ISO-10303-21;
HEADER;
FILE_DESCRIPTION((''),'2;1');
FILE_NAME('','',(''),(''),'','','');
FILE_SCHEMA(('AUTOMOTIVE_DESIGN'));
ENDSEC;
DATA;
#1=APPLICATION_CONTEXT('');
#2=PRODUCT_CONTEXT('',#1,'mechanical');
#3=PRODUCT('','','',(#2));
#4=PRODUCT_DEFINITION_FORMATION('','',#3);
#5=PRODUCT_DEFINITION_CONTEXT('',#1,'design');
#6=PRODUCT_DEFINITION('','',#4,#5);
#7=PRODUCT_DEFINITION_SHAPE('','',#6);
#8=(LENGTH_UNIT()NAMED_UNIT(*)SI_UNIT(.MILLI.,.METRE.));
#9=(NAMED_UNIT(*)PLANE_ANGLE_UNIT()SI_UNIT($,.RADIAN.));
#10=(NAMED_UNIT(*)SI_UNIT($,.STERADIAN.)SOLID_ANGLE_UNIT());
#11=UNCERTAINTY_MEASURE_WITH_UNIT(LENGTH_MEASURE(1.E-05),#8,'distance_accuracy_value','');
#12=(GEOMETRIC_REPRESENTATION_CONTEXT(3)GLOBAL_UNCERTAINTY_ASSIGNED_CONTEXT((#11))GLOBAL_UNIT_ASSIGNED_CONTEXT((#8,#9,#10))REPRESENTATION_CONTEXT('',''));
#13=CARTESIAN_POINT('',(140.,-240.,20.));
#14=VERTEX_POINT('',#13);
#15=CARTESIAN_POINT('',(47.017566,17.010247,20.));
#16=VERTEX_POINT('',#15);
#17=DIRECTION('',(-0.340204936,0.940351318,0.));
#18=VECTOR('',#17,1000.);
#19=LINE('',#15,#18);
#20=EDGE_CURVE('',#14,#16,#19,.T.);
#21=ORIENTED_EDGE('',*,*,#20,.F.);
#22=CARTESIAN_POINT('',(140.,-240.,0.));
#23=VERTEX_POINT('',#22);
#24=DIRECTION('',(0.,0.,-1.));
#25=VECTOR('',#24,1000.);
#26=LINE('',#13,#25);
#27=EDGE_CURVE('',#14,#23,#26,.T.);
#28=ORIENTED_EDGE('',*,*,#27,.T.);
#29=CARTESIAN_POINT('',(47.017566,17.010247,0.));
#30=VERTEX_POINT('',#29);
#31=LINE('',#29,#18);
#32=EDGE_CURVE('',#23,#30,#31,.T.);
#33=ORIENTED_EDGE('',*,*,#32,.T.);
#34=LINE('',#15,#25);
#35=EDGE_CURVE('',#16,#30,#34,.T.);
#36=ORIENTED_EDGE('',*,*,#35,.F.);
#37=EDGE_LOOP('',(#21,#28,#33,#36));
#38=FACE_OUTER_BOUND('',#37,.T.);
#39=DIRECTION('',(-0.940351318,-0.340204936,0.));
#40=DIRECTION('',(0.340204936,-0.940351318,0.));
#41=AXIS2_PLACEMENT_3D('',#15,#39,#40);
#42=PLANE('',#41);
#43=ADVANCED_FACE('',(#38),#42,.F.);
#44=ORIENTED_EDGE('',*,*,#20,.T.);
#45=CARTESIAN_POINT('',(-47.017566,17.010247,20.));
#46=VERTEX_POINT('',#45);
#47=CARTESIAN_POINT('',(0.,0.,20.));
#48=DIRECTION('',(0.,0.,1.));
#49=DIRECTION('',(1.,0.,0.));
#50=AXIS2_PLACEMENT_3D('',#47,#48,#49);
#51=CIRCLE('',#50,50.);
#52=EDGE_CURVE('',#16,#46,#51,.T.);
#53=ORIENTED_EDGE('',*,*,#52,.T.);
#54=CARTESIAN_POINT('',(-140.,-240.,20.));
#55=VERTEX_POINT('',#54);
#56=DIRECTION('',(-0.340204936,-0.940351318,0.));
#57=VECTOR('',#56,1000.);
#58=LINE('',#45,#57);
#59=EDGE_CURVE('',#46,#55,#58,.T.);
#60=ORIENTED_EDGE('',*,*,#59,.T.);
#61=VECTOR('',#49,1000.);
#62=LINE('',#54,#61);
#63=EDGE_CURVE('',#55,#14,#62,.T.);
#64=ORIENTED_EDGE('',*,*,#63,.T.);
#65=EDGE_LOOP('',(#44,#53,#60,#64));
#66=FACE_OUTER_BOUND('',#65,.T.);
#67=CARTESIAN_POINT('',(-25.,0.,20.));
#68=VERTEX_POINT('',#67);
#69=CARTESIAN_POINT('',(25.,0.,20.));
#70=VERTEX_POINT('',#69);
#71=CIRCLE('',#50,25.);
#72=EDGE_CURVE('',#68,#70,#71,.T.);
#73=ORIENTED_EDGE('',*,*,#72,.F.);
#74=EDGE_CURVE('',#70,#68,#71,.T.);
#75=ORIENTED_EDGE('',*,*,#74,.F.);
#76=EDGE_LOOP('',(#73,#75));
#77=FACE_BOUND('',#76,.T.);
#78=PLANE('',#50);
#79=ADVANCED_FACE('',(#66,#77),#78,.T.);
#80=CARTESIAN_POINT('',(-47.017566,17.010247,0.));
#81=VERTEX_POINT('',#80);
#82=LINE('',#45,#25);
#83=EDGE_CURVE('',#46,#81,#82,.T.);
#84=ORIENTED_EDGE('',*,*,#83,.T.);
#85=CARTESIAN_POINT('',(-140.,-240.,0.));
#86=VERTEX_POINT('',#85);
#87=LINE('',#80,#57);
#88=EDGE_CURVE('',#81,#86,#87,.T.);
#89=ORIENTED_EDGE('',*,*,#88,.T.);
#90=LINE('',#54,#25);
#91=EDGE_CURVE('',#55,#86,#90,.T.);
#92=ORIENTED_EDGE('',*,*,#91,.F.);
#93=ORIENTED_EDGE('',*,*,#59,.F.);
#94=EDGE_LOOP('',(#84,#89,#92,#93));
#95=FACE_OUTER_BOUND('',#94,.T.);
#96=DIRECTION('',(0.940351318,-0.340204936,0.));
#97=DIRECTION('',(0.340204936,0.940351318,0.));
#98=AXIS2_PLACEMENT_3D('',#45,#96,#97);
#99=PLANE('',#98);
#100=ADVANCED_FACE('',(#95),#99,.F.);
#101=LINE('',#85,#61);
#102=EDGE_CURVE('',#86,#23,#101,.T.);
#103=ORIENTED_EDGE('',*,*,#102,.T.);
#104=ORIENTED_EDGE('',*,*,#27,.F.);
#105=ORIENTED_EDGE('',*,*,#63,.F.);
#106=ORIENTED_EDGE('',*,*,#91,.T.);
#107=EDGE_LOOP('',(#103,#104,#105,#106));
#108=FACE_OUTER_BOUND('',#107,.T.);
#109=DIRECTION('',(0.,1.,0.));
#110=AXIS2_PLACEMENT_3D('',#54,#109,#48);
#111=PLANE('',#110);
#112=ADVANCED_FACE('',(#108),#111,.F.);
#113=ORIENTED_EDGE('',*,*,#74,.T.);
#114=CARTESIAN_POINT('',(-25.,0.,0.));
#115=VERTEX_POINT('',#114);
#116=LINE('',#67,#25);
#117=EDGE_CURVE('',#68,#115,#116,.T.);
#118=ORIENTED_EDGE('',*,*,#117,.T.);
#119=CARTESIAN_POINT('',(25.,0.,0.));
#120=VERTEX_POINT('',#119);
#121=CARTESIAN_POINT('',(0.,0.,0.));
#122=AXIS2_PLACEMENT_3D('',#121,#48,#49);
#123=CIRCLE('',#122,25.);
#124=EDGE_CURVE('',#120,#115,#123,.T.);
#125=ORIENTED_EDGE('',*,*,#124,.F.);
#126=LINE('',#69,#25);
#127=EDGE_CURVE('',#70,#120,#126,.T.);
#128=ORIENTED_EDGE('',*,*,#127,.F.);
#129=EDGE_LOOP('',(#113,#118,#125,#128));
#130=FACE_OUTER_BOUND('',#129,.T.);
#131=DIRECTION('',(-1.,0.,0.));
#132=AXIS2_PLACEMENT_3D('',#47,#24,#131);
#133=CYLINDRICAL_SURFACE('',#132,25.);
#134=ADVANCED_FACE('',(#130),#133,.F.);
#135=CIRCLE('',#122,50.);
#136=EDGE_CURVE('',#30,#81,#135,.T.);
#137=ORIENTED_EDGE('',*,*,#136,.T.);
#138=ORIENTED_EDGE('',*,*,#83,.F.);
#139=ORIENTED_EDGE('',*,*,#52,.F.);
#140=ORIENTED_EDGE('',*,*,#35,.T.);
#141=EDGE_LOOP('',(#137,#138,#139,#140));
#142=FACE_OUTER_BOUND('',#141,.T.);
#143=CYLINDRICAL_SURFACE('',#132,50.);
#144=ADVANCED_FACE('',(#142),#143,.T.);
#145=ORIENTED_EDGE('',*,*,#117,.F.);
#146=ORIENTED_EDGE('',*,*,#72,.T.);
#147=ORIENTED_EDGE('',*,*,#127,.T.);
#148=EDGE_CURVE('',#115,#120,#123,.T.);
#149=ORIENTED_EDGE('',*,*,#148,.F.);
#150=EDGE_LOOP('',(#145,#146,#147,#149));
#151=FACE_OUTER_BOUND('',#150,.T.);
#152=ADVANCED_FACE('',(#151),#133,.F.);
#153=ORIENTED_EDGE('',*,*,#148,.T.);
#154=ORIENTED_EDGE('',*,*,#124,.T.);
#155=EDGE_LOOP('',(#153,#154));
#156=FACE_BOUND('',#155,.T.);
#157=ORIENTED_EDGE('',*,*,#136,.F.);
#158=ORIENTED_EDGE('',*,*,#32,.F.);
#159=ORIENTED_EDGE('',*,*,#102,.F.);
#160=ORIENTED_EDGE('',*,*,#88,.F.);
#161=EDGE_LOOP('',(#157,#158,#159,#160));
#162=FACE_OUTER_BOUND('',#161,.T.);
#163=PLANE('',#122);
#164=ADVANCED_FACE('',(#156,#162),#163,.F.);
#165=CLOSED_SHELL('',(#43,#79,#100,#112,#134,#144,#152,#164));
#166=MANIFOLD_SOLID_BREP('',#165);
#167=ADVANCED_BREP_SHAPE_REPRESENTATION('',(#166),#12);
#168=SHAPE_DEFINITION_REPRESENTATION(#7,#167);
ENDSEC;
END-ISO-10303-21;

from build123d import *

# Parameters (mm, degrees)
LUG_PROFILE_SKETCH_R = 25
LUG_PLATE_20MM_DEPTH = 20


with BuildPart() as part:
    # Lug Profile Sketch → Lug Plate 20mm (new body)
    with BuildSketch(Plane.XY):
        with BuildLine():
            Line((-140, -240), (140, -240))
            Line((140, -240), (47.017565913, 17.010246783))
            ThreePointArc((47.017565913, 17.010246783), (0, 50), (-47.017565913, 17.010246783))
            Line((-47.017565913, 17.010246783), (-140, -240))
        make_face()
        Circle(LUG_PROFILE_SKETCH_R, mode=Mode.SUBTRACT)
    extrude(amount=LUG_PLATE_20MM_DEPTH)


solid = part.part
